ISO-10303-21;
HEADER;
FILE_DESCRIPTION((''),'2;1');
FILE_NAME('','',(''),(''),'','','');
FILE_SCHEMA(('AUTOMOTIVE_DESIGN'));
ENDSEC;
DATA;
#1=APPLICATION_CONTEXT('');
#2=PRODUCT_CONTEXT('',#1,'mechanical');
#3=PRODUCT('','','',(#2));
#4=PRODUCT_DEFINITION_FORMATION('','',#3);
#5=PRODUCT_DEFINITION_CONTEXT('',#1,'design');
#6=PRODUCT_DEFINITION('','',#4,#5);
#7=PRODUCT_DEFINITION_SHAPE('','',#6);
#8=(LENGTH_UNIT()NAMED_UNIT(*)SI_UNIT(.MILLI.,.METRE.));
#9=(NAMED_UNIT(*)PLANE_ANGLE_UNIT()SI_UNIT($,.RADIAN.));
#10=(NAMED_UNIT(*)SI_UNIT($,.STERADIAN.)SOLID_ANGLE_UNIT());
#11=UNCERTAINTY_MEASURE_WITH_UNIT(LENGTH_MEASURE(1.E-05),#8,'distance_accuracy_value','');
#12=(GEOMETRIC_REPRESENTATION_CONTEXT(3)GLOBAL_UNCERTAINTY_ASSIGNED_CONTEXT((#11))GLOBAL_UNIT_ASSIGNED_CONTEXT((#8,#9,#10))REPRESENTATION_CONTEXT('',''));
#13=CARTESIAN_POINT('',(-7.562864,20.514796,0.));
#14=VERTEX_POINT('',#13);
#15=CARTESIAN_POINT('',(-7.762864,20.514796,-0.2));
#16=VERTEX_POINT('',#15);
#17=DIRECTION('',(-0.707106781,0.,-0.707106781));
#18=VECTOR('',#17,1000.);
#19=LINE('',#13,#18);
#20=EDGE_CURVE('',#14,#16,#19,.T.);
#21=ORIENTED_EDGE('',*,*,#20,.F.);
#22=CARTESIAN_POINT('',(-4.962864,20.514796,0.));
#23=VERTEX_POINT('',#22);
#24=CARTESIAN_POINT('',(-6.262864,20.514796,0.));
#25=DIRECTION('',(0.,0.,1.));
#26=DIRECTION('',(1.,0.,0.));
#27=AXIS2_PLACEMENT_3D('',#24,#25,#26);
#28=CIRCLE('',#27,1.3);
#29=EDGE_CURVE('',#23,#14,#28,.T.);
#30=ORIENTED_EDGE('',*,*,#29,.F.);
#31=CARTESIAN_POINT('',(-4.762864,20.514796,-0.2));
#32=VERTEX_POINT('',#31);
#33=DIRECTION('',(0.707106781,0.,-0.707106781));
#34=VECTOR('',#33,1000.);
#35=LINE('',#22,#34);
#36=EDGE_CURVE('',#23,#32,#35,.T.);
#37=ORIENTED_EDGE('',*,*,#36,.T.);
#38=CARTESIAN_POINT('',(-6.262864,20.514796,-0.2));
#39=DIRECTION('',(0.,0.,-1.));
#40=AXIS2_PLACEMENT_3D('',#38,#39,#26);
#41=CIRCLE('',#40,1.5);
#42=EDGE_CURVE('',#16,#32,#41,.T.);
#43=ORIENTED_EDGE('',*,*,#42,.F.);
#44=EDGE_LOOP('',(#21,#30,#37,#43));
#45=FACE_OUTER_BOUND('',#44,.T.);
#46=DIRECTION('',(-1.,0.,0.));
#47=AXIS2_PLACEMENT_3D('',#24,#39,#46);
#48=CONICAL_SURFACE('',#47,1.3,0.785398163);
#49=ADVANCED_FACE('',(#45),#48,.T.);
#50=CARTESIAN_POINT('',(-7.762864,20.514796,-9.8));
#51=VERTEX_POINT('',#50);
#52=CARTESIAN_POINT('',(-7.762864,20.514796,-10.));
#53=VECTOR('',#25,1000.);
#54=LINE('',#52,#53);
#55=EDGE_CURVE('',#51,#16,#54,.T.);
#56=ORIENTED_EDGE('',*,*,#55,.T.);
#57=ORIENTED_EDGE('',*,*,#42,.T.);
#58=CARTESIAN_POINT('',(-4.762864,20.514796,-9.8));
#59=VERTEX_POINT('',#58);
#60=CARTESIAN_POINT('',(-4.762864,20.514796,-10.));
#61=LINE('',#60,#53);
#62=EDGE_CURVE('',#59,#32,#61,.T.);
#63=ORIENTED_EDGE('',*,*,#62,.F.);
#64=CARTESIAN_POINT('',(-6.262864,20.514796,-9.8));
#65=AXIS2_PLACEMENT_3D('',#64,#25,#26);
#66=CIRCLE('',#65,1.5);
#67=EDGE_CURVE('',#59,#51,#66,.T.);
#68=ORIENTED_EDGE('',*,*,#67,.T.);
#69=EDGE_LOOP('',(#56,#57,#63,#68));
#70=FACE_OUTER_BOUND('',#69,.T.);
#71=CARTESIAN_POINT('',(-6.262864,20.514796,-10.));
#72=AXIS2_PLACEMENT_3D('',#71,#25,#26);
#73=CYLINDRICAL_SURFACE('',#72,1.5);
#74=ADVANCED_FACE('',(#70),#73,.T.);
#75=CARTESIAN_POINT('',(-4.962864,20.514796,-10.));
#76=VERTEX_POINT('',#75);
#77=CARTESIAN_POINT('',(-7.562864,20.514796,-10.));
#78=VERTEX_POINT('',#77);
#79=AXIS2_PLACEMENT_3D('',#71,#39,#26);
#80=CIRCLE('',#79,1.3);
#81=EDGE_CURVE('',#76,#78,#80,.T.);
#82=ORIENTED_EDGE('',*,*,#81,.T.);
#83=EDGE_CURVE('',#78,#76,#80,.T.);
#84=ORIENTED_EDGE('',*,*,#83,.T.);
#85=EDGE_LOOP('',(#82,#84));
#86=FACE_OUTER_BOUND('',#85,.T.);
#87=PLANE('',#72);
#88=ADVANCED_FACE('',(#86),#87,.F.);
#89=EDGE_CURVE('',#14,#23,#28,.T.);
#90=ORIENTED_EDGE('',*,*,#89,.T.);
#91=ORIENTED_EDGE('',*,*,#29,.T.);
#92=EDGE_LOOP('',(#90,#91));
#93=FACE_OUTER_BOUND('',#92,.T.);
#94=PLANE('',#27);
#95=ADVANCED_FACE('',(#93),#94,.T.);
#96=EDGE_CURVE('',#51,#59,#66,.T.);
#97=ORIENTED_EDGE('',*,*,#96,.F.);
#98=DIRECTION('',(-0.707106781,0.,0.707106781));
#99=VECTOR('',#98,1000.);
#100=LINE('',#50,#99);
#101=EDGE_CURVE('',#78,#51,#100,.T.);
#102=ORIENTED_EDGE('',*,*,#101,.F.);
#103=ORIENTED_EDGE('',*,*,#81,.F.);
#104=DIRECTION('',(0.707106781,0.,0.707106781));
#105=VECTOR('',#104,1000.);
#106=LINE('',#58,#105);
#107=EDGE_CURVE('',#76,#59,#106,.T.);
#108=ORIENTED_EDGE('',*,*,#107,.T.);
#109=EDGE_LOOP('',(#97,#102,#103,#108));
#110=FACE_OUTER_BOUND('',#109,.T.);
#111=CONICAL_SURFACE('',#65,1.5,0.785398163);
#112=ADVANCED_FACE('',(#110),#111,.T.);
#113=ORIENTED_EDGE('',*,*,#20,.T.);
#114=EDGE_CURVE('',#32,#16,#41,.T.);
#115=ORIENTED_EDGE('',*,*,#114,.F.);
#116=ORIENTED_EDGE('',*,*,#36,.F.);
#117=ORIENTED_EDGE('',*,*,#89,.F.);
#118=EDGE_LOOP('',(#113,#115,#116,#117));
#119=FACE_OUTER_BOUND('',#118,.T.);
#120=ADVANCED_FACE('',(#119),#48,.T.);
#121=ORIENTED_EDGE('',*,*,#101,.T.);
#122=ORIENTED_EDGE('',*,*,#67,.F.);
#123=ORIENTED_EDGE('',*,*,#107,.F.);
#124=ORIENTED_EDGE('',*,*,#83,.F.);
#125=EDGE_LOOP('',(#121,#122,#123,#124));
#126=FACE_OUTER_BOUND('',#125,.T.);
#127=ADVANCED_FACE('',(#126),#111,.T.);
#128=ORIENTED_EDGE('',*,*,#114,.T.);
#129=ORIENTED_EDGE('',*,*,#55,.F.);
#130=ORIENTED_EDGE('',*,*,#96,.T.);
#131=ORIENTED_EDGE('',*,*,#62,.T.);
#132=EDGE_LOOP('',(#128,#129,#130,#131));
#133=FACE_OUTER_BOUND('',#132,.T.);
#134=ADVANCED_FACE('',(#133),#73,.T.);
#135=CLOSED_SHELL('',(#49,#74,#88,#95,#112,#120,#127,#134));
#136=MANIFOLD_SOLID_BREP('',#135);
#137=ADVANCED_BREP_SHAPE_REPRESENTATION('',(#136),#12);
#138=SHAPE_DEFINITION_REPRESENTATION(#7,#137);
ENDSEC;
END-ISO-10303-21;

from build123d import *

# Parameters (mm, degrees)
SKETCH2_R           = 1.5
BOSS_EXTRUDE1_DEPTH = 10
CHAMFER1_SIZE       = 0.2


with BuildPart() as part:
    # Sketch2 → Boss-Extrude1 (new body)
    with BuildSketch(Plane.XY):
        with Locations((-6.262863766, 20.514795525)):
            Circle(SKETCH2_R)
    extrude(amount=-BOSS_EXTRUDE1_DEPTH)

    # Chamfer1
    chamfer1_edges = [part.edges().sort_by_distance(p)[0] for p in [
        (-7.762863766, 20.514795525, 0),
        (-7.762863766, 20.514795525, -10),
    ]]
    chamfer(chamfer1_edges, length=CHAMFER1_SIZE)


solid = part.part
